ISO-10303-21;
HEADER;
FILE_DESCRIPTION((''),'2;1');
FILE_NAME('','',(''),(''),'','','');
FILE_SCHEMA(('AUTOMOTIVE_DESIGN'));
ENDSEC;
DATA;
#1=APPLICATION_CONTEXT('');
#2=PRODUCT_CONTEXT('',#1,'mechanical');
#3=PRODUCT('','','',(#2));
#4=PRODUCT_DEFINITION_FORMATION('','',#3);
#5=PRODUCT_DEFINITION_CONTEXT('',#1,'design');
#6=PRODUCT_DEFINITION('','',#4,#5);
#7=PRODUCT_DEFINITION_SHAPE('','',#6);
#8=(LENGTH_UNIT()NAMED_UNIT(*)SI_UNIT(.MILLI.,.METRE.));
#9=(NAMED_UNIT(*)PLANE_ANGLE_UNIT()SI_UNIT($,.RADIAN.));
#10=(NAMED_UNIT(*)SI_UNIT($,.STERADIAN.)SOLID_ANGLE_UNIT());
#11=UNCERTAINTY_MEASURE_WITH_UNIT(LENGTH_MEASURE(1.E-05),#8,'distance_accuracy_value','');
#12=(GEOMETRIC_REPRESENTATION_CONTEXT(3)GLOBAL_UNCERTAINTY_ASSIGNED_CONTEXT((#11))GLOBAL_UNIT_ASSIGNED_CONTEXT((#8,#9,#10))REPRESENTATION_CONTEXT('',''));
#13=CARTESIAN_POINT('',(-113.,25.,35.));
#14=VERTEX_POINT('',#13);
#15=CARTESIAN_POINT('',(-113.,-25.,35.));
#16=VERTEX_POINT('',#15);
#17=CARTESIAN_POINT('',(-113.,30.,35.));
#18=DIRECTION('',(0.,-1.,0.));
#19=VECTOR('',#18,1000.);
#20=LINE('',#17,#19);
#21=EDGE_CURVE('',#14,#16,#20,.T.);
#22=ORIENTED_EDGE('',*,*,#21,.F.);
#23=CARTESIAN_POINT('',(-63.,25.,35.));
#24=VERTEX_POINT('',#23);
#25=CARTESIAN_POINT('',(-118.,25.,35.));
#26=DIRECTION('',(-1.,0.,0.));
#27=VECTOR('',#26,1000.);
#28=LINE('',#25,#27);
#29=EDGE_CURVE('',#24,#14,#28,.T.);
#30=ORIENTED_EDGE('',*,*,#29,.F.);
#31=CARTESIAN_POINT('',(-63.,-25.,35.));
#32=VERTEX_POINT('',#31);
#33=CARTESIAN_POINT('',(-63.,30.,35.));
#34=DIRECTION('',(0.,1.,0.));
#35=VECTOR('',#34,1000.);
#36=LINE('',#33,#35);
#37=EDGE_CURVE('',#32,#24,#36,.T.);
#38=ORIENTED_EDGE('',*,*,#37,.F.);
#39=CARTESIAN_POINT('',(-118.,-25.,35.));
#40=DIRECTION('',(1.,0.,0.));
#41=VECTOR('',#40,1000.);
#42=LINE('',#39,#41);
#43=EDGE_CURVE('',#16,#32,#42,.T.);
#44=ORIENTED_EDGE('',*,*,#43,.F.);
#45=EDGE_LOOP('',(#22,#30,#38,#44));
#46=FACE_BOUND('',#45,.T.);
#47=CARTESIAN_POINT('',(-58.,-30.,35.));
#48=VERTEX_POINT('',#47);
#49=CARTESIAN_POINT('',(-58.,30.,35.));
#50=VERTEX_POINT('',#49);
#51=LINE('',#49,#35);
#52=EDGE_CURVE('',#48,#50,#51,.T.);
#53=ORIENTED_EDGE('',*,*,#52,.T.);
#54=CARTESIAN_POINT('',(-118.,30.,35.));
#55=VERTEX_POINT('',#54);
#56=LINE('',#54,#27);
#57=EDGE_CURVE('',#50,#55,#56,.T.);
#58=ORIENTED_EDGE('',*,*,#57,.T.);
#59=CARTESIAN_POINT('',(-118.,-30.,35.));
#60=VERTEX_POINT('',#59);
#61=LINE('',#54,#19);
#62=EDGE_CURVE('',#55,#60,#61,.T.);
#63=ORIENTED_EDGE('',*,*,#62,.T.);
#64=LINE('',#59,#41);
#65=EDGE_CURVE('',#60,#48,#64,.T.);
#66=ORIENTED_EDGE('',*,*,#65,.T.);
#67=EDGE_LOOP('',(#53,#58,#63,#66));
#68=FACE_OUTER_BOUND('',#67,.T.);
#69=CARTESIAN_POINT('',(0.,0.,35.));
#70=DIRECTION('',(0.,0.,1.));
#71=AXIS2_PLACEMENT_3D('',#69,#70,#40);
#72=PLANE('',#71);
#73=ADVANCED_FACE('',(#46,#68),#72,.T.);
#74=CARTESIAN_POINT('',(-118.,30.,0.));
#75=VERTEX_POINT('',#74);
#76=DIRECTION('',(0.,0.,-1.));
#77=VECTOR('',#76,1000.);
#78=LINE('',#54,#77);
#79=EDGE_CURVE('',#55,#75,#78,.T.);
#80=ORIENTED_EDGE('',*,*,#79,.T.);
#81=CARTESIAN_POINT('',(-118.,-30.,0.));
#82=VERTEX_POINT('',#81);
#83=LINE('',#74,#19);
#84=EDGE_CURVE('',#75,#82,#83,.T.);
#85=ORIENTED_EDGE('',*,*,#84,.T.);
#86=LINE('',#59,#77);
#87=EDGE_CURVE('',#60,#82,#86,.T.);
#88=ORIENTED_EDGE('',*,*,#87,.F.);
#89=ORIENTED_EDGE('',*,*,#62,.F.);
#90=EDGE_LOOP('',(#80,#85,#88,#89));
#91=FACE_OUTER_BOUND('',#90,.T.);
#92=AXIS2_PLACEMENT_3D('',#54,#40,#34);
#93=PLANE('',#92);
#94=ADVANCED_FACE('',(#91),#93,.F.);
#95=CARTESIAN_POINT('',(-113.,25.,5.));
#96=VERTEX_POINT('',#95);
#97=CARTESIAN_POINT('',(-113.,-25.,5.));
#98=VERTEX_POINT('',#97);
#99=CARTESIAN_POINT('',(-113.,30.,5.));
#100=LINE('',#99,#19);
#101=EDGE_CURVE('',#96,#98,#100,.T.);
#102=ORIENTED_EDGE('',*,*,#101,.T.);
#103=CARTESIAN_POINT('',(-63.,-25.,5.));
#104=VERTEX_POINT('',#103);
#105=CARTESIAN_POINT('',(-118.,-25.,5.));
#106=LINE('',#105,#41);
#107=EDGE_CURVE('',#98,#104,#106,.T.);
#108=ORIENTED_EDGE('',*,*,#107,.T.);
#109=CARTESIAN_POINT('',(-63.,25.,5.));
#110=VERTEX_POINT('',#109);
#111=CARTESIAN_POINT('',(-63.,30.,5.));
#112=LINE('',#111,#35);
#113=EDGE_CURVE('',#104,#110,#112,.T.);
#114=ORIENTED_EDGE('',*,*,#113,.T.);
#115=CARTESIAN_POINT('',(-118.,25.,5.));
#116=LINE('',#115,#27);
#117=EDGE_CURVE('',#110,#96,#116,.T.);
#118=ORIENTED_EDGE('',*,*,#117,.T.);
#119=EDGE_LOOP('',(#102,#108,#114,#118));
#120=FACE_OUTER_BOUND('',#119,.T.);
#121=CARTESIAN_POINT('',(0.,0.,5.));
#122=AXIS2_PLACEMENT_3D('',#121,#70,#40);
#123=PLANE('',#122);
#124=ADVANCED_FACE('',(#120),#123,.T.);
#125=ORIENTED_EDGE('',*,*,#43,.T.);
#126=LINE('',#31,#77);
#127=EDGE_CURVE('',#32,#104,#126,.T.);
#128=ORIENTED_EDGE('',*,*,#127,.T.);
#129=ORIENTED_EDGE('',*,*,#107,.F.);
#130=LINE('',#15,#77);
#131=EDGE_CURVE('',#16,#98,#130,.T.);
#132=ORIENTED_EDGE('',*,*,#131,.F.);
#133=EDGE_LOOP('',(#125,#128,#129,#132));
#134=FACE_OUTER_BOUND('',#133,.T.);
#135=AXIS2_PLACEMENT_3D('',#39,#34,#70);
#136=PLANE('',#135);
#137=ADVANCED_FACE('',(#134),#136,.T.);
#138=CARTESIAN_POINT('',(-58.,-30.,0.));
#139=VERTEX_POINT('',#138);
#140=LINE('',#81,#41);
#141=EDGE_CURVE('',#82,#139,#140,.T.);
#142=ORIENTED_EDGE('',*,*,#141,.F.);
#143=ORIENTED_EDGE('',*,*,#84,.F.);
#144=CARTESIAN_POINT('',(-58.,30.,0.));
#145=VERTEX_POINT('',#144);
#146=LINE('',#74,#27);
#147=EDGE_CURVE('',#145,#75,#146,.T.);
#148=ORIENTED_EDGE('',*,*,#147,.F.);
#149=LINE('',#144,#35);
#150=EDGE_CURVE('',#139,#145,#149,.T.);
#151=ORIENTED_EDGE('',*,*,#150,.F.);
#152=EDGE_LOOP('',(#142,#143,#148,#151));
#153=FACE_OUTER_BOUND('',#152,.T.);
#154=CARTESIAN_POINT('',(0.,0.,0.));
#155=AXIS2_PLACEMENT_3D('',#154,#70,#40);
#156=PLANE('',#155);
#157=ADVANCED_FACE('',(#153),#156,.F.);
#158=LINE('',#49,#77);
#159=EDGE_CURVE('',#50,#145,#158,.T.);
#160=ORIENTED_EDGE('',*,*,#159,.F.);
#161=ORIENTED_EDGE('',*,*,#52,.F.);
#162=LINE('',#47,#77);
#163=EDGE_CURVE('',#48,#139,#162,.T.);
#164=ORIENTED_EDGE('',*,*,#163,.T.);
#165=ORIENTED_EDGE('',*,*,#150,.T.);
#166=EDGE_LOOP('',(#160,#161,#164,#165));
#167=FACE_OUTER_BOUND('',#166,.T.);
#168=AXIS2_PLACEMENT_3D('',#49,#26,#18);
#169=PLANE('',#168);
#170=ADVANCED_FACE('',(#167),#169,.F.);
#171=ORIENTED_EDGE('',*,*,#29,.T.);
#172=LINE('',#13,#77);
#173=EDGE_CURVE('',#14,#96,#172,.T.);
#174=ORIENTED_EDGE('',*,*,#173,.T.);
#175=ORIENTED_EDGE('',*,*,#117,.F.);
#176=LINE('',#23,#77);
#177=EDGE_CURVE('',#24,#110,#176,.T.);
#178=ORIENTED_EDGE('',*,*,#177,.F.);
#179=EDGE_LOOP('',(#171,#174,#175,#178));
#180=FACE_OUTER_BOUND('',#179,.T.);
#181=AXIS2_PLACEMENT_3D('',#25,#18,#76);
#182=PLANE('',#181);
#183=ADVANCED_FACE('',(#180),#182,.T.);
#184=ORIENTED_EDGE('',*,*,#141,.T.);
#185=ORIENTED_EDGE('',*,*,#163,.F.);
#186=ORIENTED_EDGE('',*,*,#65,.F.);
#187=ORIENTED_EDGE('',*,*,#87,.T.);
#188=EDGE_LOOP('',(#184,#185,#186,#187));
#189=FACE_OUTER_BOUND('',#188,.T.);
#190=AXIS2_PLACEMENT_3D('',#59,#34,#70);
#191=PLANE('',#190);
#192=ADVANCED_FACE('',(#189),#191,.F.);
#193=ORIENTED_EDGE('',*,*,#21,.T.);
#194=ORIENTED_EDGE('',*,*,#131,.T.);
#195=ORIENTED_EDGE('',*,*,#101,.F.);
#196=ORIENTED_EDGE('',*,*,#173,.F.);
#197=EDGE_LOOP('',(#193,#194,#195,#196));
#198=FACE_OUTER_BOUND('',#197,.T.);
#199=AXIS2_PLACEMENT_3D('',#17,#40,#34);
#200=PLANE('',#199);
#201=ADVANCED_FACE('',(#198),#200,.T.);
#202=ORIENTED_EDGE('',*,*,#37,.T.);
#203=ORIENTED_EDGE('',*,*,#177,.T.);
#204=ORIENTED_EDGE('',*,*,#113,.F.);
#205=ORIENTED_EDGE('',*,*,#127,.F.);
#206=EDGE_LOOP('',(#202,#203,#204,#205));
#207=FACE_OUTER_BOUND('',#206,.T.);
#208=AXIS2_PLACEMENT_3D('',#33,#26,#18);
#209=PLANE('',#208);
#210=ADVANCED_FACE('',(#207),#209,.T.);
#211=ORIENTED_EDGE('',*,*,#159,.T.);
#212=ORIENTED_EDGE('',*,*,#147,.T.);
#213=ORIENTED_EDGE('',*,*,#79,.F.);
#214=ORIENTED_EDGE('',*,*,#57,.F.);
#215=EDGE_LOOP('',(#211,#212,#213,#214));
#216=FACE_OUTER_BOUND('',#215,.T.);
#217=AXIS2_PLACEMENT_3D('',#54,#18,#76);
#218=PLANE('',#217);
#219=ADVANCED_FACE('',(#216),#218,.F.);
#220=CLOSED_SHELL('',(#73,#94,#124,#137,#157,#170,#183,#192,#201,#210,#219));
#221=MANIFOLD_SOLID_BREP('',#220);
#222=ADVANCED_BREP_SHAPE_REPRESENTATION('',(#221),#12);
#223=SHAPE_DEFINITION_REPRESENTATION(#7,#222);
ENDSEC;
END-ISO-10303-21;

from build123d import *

# Parameters (mm, degrees)
SKETCH1_W           = 60
SKETCH1_H           = 60
BOSS_EXTRUDE1_DEPTH = 35
SHELL1_T            = -5


with BuildPart() as part:
    # Sketch1 → Boss-Extrude1 (new body)
    with BuildSketch(Plane.XY):
        with Locations((-88, 0)):
            Rectangle(SKETCH1_W, SKETCH1_H)
    extrude(amount=BOSS_EXTRUDE1_DEPTH)

    # Shell1
    shell1_openings = [part.faces().sort_by_distance(p)[0] for p in [
        (-88, 0, 35),
    ]]
    offset(amount=SHELL1_T, openings=shell1_openings, kind=Kind.INTERSECTION)


solid = part.part
